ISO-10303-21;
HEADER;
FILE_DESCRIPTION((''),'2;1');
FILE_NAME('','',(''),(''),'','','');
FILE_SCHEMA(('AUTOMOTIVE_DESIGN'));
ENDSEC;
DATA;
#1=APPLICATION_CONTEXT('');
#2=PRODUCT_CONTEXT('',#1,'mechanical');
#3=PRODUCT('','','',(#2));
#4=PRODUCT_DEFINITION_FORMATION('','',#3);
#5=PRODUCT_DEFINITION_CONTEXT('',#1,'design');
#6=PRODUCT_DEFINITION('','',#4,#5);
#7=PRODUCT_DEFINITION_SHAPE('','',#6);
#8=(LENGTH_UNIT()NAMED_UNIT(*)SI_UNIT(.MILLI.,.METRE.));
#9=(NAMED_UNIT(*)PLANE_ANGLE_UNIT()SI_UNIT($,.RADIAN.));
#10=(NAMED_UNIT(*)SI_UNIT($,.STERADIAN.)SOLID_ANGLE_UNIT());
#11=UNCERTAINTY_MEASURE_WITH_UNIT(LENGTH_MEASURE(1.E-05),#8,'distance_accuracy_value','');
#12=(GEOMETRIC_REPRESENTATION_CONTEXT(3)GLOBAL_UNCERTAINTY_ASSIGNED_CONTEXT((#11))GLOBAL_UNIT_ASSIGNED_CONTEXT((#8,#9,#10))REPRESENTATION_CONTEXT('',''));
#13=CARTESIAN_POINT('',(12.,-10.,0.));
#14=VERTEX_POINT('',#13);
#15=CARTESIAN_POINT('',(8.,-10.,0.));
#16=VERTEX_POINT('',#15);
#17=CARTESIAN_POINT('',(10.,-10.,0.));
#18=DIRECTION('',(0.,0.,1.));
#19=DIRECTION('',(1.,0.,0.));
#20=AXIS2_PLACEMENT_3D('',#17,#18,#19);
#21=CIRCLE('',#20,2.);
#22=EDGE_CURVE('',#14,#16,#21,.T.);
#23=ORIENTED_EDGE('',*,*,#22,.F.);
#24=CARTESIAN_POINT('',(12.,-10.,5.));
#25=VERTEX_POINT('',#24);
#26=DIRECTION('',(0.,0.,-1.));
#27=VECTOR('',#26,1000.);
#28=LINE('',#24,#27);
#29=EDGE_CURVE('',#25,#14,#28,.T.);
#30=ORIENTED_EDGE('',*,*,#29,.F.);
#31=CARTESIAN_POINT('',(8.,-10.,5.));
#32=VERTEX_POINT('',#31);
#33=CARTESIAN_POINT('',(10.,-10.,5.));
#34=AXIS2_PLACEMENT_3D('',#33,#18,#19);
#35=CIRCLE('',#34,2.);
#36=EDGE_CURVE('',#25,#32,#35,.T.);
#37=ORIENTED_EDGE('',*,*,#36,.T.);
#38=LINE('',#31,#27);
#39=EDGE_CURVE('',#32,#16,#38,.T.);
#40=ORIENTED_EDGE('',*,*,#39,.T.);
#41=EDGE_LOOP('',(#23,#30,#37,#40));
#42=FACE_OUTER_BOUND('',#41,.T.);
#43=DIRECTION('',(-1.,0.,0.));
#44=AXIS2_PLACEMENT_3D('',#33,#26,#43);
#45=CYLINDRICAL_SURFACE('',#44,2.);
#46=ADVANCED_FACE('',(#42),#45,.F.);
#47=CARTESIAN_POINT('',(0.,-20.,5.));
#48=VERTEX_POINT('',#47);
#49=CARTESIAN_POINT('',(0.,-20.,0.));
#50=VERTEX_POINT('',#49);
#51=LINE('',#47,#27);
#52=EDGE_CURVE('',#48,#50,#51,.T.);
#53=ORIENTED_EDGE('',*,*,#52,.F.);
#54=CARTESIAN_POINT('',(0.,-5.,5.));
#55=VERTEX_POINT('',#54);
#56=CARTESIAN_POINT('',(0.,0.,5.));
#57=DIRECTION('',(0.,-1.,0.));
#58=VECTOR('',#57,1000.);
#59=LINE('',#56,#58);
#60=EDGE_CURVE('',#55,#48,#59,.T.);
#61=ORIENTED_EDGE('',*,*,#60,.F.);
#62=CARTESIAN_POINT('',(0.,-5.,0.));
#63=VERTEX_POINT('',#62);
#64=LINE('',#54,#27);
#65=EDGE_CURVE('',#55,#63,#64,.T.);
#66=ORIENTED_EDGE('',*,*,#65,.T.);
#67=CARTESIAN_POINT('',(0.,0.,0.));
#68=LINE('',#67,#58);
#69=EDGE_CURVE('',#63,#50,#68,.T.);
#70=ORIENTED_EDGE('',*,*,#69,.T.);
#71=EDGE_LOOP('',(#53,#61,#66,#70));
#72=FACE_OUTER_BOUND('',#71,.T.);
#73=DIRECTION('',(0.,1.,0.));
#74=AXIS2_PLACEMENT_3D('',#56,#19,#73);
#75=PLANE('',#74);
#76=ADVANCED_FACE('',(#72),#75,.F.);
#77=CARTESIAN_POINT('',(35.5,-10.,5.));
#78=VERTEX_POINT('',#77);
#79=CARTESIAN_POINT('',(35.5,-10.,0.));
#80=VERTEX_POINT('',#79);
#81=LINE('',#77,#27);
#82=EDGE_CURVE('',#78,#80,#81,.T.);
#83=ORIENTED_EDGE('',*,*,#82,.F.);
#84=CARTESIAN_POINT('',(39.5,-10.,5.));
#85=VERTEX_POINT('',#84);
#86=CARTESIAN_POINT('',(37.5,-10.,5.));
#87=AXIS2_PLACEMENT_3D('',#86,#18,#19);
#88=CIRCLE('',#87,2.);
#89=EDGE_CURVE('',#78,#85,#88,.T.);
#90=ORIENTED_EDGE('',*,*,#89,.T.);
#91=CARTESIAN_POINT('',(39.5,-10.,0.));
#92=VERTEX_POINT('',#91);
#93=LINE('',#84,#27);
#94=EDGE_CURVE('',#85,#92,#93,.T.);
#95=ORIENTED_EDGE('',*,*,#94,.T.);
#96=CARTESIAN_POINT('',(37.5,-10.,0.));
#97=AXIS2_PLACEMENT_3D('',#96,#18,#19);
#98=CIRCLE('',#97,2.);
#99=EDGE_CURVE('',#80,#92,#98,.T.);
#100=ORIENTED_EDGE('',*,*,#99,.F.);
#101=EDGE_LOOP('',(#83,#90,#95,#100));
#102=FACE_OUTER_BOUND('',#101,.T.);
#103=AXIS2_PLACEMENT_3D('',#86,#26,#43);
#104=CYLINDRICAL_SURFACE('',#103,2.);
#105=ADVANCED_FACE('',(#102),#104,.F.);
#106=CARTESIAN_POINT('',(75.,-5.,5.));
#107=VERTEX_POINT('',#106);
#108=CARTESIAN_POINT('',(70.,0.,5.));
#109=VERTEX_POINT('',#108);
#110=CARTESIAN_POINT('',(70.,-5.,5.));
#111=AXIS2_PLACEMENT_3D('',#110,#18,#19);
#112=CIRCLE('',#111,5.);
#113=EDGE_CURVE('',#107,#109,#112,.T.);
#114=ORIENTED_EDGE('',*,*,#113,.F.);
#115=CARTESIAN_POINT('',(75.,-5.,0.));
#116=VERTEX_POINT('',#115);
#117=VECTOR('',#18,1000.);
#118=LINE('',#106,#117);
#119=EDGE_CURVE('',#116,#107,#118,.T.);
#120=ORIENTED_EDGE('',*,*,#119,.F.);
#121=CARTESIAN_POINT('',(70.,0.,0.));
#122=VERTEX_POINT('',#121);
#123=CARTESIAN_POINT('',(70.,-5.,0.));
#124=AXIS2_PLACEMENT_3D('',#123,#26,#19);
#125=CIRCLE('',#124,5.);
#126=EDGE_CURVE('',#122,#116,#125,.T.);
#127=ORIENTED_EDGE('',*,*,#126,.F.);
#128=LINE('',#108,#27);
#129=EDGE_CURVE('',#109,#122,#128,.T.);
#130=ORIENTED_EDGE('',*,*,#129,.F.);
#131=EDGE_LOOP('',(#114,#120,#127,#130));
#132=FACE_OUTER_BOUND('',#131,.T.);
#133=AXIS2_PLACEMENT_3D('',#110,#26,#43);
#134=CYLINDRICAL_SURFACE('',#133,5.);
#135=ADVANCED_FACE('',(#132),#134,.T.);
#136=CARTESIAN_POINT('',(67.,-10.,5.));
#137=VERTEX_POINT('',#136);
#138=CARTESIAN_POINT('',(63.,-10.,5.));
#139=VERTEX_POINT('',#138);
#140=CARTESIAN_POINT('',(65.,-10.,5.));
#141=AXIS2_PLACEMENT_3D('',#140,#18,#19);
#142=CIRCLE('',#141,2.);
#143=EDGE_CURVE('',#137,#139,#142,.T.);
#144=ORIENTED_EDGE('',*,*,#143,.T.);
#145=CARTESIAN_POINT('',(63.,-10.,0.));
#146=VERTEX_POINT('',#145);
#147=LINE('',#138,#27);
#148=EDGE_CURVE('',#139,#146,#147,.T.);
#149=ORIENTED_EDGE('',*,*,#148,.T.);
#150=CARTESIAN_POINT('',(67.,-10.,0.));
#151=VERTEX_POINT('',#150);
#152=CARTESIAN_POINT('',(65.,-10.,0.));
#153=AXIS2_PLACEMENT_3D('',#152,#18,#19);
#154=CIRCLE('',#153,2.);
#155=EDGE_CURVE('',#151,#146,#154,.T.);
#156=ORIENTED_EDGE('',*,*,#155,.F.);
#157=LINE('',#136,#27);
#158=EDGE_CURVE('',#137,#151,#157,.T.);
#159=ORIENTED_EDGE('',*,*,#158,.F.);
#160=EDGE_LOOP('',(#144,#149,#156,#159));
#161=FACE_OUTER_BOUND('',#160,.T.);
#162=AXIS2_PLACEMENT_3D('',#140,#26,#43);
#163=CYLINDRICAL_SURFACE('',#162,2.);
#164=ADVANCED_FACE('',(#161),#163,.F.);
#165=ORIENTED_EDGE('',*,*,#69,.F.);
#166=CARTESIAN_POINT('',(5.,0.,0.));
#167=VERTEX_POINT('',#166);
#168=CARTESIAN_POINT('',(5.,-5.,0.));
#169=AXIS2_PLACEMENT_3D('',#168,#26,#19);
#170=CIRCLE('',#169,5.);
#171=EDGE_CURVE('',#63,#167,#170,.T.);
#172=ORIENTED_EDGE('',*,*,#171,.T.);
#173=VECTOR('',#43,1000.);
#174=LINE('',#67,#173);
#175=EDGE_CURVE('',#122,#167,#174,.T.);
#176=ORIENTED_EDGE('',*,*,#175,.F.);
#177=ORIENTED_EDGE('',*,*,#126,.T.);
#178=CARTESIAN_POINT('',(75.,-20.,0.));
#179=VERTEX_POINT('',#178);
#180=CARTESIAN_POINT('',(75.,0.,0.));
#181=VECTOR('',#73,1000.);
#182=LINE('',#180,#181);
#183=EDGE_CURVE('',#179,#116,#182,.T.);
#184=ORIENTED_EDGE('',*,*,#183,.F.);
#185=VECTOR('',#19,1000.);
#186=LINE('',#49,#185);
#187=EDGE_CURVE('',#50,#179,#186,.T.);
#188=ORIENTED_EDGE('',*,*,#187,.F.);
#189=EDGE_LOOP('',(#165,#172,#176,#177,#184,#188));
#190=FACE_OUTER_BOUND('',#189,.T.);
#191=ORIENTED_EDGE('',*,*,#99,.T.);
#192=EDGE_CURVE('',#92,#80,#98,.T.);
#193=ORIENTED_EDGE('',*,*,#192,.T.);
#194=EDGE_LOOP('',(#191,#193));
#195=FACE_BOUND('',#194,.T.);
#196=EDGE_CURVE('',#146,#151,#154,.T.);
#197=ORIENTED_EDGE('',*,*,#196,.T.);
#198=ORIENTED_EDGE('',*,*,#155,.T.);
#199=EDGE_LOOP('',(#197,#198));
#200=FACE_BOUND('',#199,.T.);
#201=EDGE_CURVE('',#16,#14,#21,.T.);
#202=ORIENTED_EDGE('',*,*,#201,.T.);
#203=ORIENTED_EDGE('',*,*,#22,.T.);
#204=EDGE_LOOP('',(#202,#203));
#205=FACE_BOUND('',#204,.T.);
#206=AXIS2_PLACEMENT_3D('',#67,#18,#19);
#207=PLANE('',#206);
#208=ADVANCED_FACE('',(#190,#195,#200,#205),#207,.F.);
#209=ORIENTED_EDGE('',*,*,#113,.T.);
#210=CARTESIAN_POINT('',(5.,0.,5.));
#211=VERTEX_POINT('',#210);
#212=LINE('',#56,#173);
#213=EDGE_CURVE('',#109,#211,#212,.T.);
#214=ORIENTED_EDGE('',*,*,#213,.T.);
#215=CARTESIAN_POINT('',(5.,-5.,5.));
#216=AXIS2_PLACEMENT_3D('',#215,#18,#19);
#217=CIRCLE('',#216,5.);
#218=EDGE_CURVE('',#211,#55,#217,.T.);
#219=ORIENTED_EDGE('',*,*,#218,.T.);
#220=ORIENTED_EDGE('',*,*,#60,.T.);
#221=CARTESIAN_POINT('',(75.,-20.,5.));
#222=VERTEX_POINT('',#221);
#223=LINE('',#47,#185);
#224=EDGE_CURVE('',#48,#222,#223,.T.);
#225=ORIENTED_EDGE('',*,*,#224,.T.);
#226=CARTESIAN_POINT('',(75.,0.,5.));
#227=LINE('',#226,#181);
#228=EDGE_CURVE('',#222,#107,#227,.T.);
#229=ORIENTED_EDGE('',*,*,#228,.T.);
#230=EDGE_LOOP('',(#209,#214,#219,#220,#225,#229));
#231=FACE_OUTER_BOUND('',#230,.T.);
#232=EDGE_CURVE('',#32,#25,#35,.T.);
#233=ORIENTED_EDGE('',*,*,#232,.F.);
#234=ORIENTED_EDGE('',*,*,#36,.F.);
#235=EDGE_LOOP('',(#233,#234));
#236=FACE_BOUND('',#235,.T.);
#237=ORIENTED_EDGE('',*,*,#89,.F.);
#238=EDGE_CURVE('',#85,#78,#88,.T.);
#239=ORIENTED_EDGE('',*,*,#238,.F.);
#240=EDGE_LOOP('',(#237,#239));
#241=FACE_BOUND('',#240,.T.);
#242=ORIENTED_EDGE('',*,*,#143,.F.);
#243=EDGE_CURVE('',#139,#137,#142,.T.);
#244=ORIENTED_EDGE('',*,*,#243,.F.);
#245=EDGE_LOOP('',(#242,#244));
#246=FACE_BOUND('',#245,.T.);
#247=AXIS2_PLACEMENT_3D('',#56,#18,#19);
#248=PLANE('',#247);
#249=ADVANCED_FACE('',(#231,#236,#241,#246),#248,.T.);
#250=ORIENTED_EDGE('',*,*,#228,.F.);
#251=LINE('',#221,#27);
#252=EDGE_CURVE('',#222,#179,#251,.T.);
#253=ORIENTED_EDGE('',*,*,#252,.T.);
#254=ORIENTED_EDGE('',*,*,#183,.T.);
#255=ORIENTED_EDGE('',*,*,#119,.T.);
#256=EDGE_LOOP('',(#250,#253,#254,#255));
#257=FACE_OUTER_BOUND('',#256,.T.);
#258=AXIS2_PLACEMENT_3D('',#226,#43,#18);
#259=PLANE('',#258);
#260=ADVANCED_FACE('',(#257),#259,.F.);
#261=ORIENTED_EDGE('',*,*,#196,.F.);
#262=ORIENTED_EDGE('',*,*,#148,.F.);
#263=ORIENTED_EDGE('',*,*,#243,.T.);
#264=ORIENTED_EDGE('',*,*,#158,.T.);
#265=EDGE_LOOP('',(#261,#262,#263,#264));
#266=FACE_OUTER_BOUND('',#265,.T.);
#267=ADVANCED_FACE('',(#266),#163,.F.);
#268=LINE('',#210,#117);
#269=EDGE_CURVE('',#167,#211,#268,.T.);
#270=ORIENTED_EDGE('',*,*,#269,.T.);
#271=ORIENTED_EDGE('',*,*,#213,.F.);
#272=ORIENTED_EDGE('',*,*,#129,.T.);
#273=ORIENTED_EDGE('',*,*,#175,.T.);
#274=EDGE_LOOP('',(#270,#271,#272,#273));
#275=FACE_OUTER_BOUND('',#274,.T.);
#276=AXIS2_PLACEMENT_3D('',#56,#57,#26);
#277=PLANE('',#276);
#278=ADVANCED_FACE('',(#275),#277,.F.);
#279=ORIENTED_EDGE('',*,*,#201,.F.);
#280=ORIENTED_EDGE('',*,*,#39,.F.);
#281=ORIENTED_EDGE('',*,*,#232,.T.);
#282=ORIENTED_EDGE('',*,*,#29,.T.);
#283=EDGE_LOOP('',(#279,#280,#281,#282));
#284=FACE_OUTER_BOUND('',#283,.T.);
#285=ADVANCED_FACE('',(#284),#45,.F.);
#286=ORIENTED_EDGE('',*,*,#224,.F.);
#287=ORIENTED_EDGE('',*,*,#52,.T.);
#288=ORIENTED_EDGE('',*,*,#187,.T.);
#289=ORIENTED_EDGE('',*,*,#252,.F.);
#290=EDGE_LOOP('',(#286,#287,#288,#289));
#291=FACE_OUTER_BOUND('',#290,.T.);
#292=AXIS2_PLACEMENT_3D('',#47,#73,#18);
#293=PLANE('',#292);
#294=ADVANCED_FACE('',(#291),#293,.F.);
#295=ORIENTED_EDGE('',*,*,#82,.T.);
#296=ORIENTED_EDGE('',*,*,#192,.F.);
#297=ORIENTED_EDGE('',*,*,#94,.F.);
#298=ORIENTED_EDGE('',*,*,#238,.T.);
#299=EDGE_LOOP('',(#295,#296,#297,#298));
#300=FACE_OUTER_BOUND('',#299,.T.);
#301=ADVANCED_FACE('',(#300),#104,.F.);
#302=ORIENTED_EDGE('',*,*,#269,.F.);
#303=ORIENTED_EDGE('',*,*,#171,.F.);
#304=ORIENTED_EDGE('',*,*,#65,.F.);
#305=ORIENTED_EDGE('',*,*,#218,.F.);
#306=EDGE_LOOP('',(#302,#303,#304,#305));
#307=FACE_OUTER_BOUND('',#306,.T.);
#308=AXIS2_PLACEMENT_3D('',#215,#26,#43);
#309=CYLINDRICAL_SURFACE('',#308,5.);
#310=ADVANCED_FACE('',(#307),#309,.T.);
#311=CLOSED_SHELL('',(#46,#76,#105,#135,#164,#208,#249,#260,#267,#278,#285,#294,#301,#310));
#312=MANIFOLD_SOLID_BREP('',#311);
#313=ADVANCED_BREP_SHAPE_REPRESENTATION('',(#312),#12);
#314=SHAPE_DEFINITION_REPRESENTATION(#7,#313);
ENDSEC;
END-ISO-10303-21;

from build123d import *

# Parameters (mm, degrees)
SKETCH1_W           = 75
SKETCH1_H           = 20
SKETCH1_R           = 2
BOSS_EXTRUDE1_DEPTH = 5
FILLET1_R           = 5


with BuildPart() as part:
    # Sketch1 → Boss-Extrude1 (new body)
    with BuildSketch(Plane.XY):
        with Locations((37.5, -10)):
            Rectangle(SKETCH1_W, SKETCH1_H)
        with Locations((10, -10)):
            Circle(SKETCH1_R, mode=Mode.SUBTRACT)
        with Locations((65, -10)):
            Circle(SKETCH1_R, mode=Mode.SUBTRACT)
        with Locations((37.5, -10)):
            Circle(SKETCH1_R, mode=Mode.SUBTRACT)
    extrude(amount=BOSS_EXTRUDE1_DEPTH)

    # Fillet1
    fillet1_edges = [part.edges().sort_by_distance(p)[0] for p in [
        (0, 0, 2.5),
        (75, 0, 2.5),
    ]]
    fillet(fillet1_edges, radius=FILLET1_R)


solid = part.part
